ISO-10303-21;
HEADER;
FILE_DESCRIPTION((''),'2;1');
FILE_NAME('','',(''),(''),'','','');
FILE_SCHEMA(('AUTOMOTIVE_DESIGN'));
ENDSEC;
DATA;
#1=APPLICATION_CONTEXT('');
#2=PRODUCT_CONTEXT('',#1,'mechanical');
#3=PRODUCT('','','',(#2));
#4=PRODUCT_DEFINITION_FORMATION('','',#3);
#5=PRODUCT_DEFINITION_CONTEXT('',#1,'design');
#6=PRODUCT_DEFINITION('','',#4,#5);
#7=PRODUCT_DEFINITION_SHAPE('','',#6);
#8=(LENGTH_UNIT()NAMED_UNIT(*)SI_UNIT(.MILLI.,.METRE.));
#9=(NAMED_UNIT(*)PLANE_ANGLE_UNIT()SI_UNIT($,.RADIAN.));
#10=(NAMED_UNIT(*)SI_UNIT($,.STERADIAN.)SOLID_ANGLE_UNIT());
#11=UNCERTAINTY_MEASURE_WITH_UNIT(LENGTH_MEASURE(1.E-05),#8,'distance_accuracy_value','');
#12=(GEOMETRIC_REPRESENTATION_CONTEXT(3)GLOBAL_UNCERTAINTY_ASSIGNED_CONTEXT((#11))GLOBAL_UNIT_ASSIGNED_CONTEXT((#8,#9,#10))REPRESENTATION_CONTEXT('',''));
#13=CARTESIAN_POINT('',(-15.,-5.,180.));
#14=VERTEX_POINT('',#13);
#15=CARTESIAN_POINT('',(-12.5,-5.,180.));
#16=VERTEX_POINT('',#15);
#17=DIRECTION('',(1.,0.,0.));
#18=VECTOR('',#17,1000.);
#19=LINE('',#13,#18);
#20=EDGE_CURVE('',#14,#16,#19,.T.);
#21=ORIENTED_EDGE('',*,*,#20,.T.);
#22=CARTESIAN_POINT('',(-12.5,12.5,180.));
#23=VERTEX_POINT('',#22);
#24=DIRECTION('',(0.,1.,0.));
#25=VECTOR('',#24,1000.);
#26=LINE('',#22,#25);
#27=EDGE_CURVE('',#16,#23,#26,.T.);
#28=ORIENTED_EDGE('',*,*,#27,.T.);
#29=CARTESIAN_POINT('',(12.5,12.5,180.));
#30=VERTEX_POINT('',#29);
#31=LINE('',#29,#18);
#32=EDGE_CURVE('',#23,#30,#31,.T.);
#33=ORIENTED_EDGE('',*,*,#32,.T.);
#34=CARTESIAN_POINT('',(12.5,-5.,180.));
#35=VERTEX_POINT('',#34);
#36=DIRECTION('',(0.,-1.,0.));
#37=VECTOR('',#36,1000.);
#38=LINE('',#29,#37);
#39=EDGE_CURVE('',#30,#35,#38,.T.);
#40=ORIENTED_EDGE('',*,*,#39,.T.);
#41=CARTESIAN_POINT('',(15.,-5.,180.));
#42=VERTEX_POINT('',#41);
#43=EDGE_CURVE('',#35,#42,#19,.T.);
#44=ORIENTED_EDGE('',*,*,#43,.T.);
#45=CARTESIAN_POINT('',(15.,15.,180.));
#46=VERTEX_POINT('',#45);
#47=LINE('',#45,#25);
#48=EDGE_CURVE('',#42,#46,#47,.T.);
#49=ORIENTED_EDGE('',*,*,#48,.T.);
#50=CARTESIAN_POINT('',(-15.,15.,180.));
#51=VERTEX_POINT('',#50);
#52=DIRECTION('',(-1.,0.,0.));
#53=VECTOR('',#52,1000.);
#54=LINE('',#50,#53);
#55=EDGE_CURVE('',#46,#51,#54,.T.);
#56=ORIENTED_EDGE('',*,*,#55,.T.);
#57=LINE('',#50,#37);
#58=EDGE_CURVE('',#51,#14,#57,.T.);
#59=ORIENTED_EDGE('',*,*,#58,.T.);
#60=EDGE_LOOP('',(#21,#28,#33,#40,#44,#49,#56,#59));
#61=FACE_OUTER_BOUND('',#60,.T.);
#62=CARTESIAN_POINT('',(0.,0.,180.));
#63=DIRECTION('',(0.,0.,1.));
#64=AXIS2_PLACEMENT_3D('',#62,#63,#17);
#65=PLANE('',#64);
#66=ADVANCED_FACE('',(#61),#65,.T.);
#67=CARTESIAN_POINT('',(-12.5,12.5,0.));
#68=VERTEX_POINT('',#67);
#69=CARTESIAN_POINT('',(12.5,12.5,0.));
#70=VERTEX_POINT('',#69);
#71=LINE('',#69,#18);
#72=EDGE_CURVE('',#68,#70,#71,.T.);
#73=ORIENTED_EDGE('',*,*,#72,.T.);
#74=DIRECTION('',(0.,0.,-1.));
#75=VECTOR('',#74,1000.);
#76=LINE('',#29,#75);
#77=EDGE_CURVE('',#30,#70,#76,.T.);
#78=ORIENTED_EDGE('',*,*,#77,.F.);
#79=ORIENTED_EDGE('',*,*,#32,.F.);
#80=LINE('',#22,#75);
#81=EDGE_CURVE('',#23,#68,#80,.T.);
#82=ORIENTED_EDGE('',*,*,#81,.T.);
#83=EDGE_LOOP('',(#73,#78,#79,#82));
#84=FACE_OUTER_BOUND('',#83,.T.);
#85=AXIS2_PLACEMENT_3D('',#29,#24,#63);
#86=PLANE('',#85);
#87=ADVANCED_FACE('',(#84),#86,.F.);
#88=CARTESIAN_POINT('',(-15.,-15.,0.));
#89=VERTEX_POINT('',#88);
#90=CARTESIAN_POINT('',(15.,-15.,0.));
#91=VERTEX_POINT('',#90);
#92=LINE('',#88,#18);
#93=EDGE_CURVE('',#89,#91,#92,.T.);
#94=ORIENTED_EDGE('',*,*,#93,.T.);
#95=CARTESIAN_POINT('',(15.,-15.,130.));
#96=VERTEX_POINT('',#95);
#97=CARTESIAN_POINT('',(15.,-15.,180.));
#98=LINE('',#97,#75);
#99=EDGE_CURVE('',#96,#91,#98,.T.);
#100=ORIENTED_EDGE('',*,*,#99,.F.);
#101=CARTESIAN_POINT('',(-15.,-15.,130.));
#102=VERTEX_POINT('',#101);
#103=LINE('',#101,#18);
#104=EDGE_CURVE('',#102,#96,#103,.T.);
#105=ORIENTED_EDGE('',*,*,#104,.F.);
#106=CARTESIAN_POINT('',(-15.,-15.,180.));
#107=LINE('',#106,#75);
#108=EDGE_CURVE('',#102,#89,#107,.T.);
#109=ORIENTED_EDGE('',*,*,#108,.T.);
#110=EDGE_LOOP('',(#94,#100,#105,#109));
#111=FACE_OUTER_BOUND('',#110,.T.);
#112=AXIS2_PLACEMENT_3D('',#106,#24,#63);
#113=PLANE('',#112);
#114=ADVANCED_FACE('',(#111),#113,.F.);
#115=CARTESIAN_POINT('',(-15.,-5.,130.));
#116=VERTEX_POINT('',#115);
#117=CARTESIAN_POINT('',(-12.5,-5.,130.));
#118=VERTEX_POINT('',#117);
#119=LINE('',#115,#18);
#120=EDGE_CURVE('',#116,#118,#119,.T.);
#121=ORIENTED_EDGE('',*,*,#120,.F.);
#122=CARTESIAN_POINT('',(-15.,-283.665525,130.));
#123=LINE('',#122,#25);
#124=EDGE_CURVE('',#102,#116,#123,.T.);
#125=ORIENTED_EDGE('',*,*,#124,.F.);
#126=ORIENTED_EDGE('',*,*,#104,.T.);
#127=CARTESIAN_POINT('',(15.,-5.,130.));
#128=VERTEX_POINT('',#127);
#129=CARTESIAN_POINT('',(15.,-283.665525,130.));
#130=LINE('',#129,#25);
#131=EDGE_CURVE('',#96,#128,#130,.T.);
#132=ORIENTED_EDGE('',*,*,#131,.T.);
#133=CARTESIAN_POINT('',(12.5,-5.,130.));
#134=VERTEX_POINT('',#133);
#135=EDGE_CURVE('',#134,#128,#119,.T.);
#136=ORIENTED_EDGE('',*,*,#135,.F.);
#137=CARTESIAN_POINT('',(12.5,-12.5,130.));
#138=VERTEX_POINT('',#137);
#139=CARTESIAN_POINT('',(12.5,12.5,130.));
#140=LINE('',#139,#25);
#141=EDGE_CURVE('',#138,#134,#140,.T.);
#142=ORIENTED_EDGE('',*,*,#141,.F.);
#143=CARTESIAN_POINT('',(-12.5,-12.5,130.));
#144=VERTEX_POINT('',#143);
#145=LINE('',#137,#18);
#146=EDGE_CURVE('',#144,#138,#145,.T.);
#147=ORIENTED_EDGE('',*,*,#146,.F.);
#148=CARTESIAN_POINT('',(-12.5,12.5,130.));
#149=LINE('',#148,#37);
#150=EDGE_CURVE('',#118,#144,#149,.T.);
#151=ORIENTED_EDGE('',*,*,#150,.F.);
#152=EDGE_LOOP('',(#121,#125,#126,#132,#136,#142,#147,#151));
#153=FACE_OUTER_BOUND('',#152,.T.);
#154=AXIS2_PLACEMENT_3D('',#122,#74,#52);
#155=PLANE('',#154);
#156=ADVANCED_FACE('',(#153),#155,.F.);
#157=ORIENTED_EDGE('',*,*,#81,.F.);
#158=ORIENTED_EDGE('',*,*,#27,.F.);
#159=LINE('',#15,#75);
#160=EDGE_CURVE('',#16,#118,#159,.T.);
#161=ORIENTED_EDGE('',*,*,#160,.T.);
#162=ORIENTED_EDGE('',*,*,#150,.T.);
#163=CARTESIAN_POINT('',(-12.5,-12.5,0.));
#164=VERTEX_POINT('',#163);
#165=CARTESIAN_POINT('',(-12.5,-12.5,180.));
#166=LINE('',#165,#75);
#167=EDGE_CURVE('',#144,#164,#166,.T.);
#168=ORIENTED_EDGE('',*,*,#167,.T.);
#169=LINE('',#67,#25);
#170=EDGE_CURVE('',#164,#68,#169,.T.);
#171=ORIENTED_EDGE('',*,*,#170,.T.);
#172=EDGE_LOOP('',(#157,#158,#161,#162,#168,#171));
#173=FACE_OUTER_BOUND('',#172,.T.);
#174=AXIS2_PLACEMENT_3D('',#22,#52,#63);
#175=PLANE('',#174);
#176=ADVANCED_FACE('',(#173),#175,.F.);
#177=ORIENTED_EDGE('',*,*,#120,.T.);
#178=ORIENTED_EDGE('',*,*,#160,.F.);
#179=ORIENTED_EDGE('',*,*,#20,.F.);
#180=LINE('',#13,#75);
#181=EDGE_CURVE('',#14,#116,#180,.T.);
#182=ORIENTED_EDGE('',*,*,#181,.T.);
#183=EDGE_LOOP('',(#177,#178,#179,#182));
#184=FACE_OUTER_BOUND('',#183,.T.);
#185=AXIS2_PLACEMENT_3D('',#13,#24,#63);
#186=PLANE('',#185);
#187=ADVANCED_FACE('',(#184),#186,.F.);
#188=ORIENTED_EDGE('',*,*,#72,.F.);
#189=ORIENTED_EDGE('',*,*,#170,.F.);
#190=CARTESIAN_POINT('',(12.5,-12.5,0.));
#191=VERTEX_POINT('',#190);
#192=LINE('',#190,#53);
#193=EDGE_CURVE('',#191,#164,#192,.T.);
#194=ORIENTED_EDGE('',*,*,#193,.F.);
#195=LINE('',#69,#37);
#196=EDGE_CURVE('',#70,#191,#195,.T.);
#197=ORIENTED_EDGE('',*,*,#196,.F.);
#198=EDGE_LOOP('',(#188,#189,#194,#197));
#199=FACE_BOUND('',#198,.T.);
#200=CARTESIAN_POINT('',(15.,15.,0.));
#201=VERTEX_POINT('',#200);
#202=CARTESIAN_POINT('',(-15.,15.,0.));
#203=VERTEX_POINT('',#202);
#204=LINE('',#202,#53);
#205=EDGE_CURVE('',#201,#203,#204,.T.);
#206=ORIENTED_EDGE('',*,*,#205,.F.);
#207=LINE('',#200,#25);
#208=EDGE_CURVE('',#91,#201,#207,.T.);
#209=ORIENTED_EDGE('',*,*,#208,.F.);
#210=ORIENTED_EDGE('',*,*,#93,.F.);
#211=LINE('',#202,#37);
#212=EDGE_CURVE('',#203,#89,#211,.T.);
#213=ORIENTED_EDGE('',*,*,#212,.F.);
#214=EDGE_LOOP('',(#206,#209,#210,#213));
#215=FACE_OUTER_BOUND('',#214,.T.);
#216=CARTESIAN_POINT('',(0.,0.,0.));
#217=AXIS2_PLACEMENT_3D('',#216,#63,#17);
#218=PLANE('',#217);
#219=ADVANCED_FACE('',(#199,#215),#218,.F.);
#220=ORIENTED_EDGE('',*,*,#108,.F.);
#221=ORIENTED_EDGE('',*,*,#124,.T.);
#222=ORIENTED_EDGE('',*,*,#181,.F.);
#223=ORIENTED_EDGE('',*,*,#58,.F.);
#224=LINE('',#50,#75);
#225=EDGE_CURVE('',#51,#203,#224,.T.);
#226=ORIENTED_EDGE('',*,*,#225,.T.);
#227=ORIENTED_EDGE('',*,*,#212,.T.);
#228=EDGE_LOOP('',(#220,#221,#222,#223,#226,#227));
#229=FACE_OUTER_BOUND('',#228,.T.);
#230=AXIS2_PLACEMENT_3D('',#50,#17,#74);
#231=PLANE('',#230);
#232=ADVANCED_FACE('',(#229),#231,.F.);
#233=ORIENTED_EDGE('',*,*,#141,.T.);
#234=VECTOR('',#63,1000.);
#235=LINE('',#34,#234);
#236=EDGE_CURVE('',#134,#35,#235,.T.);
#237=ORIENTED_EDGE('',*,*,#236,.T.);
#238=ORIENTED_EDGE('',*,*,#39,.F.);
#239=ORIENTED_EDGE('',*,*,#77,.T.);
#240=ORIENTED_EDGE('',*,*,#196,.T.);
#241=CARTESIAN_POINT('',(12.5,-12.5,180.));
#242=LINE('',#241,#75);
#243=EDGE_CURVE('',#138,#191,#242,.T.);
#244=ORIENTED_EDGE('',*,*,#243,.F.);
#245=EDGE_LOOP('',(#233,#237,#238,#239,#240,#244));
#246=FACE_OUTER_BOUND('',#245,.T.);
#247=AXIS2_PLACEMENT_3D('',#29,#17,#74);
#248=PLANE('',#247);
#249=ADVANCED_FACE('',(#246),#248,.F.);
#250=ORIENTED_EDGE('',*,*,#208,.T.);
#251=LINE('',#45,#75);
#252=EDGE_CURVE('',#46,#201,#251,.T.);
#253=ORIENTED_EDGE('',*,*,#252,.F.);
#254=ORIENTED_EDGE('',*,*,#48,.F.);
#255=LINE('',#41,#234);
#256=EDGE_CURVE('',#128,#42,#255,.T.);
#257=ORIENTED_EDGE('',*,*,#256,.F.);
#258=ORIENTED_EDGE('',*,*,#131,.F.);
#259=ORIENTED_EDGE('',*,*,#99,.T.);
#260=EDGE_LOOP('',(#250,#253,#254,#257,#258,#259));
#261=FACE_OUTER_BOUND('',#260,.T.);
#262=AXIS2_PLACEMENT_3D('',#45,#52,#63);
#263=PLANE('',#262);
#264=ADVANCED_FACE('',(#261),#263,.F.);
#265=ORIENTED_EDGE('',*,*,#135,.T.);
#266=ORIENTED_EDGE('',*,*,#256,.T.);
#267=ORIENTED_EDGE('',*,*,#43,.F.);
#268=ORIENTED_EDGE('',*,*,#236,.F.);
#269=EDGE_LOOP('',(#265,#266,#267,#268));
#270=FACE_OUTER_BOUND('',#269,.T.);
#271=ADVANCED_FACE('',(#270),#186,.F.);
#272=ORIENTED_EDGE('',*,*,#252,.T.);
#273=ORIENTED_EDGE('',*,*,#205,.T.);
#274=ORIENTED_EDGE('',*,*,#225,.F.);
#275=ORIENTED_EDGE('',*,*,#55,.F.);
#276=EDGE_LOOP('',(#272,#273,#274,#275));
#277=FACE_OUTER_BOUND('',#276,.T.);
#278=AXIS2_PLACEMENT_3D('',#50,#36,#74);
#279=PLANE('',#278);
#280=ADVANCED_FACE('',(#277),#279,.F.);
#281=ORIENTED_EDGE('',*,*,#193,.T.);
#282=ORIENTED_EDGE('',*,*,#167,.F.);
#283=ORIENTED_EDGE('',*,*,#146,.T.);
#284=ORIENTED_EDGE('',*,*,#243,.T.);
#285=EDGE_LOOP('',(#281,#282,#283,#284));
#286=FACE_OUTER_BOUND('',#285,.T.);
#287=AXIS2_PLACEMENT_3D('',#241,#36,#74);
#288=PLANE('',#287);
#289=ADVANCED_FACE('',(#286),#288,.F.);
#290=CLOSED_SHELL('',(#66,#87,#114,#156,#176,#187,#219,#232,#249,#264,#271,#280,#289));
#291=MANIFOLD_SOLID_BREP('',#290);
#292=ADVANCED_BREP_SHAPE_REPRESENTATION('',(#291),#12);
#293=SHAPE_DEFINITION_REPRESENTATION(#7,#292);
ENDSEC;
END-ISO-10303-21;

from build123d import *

# Parameters (mm, degrees)
SKETCH1_W               = 30
SKETCH1_H               = 30
BOSS_EXTRUDE1_DEPTH     = 180
SKETCH5_W               = 25
SKETCH5_H               = 25
CUT_EXTRUDE4_DEPTH      = 182.245689604
CUT_EXTRUDE3_DEPTH      = 184.098334236
CUT_EXTRUDE3_DEPTH_BACK = 10


with BuildPart() as part:
    # Sketch1 → Boss-Extrude1 (new body)
    with BuildSketch(Plane.XY):
        Rectangle(SKETCH1_W, SKETCH1_H)
    extrude(amount=BOSS_EXTRUDE1_DEPTH)

    # Sketch5 → Cut-Extrude4 (cut, through all)
    with BuildSketch(Plane(origin=(0, 0, 0), x_dir=(-1, 0, 0), z_dir=(0, 0, -1))):
        Rectangle(SKETCH5_W, SKETCH5_H)
    extrude(amount=-CUT_EXTRUDE4_DEPTH, mode=Mode.SUBTRACT)

    # Sketch3 → Cut-Extrude3 (cut, two sides: drawn at the far end of the back side and taken through both)
    with BuildSketch(Plane.XZ.offset(15).offset(-CUT_EXTRUDE3_DEPTH_BACK)):
        Polygon((-389.965751818, 130), (-15, 130), (15, 130), (15, 180), (15, 554.965751818), (-527.902959777, 1072.318278062), (-932.868711595, 647.352526244), align=None)
    extrude(amount=CUT_EXTRUDE3_DEPTH + CUT_EXTRUDE3_DEPTH_BACK, mode=Mode.SUBTRACT)


solid = part.part
